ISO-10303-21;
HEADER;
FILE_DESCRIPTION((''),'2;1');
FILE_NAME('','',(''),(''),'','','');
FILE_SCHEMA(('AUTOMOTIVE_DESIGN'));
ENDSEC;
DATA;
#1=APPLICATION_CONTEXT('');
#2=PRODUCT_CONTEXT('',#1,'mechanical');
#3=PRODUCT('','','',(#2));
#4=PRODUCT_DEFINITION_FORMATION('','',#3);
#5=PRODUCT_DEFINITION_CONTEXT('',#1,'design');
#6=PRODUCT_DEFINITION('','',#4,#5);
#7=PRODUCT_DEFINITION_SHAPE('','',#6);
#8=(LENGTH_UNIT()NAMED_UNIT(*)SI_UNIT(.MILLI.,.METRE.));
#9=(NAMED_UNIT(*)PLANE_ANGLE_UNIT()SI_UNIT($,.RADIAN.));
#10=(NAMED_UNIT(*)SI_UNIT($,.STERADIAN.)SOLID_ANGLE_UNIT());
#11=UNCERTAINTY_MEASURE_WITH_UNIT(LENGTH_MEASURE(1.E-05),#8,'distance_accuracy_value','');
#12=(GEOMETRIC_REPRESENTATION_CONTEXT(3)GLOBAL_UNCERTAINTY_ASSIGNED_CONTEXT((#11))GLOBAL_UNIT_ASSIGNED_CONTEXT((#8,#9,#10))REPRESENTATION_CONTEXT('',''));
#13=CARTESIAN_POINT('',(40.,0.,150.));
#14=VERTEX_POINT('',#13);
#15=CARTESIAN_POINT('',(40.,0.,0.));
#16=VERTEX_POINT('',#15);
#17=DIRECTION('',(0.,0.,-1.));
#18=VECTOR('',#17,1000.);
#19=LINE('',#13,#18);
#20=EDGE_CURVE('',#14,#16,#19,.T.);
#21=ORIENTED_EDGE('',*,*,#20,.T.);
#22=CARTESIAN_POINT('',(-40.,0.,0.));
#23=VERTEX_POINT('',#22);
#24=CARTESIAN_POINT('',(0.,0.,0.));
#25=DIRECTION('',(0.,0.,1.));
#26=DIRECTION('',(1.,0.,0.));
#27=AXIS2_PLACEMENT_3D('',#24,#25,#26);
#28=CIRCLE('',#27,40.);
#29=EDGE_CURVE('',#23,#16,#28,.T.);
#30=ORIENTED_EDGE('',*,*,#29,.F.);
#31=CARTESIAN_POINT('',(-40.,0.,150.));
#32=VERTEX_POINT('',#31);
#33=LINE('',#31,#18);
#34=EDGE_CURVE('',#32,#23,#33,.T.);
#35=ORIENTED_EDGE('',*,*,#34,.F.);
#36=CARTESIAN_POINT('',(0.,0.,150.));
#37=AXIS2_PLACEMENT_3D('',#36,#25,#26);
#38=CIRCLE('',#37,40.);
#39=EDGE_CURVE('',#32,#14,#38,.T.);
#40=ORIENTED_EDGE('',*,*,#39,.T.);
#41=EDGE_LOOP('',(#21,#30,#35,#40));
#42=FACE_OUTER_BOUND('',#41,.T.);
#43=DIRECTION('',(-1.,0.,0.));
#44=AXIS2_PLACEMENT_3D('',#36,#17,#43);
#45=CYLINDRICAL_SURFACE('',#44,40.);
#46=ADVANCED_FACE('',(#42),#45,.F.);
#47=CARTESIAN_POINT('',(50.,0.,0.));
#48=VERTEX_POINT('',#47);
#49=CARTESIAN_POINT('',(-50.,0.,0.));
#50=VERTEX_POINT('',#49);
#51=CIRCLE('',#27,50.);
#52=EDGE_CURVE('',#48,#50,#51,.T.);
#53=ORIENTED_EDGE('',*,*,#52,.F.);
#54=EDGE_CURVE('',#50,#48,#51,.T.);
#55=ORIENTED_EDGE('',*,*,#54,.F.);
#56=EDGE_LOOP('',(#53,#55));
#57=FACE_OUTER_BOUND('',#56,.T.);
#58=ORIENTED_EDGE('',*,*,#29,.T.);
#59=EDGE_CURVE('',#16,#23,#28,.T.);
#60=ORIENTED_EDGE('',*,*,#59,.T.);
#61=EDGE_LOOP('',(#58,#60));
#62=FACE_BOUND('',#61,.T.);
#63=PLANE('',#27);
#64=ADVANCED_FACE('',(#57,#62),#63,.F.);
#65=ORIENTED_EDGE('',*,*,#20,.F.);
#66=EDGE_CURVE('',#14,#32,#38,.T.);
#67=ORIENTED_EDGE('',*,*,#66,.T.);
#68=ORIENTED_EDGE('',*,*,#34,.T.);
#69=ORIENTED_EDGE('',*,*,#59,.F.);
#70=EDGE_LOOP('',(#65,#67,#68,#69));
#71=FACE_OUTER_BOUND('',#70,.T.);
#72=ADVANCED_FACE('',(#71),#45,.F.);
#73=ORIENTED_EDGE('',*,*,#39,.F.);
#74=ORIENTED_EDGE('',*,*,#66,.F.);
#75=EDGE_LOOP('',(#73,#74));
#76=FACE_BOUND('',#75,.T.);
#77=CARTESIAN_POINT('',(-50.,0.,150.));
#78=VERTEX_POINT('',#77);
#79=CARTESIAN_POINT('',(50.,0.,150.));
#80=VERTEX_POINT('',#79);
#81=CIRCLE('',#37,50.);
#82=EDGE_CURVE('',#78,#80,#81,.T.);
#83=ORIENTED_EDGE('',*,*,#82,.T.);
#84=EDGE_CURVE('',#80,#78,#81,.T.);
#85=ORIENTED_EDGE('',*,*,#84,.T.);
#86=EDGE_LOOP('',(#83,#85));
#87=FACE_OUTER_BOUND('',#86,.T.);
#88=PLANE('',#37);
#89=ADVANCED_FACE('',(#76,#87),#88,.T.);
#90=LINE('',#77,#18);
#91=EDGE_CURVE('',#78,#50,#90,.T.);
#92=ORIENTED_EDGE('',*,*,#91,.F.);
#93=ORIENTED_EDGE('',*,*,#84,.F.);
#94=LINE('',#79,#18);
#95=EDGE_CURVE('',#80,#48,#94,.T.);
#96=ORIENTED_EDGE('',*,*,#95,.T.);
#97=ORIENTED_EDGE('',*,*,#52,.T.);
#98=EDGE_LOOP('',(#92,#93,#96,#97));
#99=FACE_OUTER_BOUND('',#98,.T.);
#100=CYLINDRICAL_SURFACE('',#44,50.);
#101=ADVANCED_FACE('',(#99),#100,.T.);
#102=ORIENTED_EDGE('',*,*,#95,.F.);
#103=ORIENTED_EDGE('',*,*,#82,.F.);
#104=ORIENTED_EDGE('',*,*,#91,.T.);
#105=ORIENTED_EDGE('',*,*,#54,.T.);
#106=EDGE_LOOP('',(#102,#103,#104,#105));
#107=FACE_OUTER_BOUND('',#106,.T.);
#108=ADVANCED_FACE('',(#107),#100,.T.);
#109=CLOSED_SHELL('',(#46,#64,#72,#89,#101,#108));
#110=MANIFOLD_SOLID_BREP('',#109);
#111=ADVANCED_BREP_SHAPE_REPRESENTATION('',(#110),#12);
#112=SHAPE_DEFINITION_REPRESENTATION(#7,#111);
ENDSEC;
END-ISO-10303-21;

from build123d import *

# Parameters (mm, degrees)
SKETCH1_R           = 50
SKETCH1_R_2         = 40
BOSS_EXTRUDE1_DEPTH = 150


with BuildPart() as part:
    # Sketch1 → Boss-Extrude1 (new body)
    with BuildSketch(Plane.XY):
        Circle(SKETCH1_R)
        Circle(SKETCH1_R_2, mode=Mode.SUBTRACT)
    extrude(amount=BOSS_EXTRUDE1_DEPTH)


solid = part.part
